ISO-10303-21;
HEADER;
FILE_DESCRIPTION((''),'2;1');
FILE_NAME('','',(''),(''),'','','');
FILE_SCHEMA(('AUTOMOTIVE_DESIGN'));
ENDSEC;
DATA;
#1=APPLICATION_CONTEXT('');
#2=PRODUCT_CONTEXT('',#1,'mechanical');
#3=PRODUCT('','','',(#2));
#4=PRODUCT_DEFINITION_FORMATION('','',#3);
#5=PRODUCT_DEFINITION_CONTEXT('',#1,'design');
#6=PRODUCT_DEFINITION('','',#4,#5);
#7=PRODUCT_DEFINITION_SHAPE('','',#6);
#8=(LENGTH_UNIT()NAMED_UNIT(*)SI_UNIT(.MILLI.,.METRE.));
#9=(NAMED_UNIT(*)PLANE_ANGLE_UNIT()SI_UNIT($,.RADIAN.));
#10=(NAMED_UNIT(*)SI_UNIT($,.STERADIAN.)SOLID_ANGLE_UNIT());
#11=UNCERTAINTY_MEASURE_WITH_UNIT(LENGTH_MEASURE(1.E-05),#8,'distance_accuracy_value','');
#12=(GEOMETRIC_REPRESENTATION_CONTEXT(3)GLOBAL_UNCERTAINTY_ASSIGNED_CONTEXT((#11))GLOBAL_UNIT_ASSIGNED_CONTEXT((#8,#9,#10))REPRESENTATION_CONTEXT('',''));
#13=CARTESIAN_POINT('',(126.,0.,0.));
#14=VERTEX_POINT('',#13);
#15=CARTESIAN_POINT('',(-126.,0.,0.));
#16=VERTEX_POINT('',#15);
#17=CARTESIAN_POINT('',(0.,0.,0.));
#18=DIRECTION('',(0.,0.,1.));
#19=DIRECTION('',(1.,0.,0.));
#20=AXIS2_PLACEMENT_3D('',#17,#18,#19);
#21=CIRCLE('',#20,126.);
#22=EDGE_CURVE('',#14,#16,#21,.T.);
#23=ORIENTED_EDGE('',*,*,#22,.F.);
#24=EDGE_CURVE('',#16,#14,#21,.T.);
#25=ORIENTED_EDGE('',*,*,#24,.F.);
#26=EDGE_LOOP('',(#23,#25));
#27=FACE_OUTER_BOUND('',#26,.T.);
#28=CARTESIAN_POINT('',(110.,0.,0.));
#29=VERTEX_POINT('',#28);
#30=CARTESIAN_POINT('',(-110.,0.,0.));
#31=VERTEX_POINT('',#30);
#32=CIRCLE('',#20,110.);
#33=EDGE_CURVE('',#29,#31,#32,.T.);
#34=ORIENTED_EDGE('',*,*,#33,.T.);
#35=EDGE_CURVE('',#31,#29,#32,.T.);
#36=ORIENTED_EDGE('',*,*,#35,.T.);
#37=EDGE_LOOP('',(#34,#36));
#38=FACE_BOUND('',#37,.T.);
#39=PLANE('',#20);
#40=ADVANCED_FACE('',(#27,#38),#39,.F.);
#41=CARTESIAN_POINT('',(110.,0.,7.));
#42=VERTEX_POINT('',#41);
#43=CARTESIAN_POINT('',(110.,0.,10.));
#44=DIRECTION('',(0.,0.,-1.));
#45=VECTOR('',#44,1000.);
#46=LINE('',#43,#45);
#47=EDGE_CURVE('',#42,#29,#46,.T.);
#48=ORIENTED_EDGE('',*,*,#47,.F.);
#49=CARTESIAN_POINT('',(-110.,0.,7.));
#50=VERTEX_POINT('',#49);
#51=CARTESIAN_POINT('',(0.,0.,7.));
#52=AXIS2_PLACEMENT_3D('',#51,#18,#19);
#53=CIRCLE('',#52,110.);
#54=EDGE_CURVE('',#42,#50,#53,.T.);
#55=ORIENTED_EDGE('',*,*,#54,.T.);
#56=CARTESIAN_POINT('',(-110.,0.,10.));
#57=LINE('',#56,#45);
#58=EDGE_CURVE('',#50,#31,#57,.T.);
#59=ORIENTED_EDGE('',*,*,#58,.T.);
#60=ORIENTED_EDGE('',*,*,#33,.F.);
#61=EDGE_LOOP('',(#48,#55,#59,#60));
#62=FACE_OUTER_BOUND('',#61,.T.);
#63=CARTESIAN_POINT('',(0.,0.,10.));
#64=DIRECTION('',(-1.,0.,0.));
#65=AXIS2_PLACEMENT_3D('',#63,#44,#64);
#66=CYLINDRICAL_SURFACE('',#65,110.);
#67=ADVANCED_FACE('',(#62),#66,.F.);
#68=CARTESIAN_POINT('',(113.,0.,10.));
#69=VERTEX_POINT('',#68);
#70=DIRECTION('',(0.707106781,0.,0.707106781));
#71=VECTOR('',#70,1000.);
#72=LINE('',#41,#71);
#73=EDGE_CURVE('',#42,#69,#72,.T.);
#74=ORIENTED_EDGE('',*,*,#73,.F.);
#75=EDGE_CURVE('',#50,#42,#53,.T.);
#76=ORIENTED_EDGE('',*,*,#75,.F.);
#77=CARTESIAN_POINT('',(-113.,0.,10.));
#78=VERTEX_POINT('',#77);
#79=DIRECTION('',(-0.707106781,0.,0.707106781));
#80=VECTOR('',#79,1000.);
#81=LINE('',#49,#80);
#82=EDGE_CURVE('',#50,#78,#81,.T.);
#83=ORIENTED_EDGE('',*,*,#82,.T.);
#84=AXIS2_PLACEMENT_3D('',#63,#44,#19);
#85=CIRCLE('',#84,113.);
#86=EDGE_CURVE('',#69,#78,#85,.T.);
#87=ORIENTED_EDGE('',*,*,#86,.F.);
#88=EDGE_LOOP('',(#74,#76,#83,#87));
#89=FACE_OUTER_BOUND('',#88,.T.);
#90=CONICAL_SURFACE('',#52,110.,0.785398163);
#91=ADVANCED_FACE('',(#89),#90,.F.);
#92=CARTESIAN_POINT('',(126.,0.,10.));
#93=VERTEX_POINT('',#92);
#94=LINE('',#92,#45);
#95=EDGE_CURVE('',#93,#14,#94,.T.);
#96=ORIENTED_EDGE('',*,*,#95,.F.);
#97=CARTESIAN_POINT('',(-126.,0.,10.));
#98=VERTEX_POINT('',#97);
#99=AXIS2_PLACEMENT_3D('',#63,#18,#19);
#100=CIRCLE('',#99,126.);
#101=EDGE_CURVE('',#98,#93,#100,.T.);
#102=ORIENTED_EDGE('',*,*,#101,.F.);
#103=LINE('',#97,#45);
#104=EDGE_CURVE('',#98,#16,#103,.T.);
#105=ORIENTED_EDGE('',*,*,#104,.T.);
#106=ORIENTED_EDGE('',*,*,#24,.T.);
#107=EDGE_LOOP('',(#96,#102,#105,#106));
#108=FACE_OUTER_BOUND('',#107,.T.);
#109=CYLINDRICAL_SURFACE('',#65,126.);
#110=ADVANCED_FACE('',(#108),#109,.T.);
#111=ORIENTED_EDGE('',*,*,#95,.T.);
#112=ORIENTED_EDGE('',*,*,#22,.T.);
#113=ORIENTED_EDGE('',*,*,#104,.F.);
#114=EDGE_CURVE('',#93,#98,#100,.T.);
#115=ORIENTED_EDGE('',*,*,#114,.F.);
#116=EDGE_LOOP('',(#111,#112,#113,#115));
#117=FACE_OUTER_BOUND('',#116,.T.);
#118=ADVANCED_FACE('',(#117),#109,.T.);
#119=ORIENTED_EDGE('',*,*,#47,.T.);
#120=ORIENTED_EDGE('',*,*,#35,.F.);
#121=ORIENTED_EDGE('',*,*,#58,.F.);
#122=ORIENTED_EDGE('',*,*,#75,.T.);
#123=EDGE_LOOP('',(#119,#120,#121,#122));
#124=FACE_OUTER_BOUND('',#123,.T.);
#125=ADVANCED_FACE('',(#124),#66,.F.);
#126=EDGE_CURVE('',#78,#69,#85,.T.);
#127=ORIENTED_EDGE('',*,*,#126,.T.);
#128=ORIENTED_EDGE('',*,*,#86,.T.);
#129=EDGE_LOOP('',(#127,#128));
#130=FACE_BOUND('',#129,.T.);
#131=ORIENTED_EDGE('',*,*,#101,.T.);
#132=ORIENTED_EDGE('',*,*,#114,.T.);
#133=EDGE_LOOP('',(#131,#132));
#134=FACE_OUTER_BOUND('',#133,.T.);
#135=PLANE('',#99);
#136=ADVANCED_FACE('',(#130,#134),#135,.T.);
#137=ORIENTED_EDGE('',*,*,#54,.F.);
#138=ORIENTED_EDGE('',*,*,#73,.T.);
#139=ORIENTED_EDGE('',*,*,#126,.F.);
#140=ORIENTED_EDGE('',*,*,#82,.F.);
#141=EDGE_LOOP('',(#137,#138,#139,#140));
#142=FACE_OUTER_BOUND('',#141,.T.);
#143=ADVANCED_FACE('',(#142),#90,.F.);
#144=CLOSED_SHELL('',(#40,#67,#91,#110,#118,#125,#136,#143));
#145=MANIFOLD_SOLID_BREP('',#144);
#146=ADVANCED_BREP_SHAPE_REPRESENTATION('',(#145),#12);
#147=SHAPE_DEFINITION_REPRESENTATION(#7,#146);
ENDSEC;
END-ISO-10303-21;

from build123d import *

# Parameters (mm, degrees)
SKETCH1_R           = 126
SKETCH1_R_2         = 110
BOSS_EXTRUDE1_DEPTH = 10
CHAMFER1_SIZE       = 3


with BuildPart() as part:
    # Sketch1 → Boss-Extrude1 (new body)
    with BuildSketch(Plane.XY):
        Circle(SKETCH1_R)
        Circle(SKETCH1_R_2, mode=Mode.SUBTRACT)
    extrude(amount=BOSS_EXTRUDE1_DEPTH)

    # Chamfer1
    chamfer1_edges = [part.edges().sort_by_distance(p)[0] for p in [
        (-110, 0, 10),
    ]]
    chamfer(chamfer1_edges, length=CHAMFER1_SIZE)


solid = part.part
